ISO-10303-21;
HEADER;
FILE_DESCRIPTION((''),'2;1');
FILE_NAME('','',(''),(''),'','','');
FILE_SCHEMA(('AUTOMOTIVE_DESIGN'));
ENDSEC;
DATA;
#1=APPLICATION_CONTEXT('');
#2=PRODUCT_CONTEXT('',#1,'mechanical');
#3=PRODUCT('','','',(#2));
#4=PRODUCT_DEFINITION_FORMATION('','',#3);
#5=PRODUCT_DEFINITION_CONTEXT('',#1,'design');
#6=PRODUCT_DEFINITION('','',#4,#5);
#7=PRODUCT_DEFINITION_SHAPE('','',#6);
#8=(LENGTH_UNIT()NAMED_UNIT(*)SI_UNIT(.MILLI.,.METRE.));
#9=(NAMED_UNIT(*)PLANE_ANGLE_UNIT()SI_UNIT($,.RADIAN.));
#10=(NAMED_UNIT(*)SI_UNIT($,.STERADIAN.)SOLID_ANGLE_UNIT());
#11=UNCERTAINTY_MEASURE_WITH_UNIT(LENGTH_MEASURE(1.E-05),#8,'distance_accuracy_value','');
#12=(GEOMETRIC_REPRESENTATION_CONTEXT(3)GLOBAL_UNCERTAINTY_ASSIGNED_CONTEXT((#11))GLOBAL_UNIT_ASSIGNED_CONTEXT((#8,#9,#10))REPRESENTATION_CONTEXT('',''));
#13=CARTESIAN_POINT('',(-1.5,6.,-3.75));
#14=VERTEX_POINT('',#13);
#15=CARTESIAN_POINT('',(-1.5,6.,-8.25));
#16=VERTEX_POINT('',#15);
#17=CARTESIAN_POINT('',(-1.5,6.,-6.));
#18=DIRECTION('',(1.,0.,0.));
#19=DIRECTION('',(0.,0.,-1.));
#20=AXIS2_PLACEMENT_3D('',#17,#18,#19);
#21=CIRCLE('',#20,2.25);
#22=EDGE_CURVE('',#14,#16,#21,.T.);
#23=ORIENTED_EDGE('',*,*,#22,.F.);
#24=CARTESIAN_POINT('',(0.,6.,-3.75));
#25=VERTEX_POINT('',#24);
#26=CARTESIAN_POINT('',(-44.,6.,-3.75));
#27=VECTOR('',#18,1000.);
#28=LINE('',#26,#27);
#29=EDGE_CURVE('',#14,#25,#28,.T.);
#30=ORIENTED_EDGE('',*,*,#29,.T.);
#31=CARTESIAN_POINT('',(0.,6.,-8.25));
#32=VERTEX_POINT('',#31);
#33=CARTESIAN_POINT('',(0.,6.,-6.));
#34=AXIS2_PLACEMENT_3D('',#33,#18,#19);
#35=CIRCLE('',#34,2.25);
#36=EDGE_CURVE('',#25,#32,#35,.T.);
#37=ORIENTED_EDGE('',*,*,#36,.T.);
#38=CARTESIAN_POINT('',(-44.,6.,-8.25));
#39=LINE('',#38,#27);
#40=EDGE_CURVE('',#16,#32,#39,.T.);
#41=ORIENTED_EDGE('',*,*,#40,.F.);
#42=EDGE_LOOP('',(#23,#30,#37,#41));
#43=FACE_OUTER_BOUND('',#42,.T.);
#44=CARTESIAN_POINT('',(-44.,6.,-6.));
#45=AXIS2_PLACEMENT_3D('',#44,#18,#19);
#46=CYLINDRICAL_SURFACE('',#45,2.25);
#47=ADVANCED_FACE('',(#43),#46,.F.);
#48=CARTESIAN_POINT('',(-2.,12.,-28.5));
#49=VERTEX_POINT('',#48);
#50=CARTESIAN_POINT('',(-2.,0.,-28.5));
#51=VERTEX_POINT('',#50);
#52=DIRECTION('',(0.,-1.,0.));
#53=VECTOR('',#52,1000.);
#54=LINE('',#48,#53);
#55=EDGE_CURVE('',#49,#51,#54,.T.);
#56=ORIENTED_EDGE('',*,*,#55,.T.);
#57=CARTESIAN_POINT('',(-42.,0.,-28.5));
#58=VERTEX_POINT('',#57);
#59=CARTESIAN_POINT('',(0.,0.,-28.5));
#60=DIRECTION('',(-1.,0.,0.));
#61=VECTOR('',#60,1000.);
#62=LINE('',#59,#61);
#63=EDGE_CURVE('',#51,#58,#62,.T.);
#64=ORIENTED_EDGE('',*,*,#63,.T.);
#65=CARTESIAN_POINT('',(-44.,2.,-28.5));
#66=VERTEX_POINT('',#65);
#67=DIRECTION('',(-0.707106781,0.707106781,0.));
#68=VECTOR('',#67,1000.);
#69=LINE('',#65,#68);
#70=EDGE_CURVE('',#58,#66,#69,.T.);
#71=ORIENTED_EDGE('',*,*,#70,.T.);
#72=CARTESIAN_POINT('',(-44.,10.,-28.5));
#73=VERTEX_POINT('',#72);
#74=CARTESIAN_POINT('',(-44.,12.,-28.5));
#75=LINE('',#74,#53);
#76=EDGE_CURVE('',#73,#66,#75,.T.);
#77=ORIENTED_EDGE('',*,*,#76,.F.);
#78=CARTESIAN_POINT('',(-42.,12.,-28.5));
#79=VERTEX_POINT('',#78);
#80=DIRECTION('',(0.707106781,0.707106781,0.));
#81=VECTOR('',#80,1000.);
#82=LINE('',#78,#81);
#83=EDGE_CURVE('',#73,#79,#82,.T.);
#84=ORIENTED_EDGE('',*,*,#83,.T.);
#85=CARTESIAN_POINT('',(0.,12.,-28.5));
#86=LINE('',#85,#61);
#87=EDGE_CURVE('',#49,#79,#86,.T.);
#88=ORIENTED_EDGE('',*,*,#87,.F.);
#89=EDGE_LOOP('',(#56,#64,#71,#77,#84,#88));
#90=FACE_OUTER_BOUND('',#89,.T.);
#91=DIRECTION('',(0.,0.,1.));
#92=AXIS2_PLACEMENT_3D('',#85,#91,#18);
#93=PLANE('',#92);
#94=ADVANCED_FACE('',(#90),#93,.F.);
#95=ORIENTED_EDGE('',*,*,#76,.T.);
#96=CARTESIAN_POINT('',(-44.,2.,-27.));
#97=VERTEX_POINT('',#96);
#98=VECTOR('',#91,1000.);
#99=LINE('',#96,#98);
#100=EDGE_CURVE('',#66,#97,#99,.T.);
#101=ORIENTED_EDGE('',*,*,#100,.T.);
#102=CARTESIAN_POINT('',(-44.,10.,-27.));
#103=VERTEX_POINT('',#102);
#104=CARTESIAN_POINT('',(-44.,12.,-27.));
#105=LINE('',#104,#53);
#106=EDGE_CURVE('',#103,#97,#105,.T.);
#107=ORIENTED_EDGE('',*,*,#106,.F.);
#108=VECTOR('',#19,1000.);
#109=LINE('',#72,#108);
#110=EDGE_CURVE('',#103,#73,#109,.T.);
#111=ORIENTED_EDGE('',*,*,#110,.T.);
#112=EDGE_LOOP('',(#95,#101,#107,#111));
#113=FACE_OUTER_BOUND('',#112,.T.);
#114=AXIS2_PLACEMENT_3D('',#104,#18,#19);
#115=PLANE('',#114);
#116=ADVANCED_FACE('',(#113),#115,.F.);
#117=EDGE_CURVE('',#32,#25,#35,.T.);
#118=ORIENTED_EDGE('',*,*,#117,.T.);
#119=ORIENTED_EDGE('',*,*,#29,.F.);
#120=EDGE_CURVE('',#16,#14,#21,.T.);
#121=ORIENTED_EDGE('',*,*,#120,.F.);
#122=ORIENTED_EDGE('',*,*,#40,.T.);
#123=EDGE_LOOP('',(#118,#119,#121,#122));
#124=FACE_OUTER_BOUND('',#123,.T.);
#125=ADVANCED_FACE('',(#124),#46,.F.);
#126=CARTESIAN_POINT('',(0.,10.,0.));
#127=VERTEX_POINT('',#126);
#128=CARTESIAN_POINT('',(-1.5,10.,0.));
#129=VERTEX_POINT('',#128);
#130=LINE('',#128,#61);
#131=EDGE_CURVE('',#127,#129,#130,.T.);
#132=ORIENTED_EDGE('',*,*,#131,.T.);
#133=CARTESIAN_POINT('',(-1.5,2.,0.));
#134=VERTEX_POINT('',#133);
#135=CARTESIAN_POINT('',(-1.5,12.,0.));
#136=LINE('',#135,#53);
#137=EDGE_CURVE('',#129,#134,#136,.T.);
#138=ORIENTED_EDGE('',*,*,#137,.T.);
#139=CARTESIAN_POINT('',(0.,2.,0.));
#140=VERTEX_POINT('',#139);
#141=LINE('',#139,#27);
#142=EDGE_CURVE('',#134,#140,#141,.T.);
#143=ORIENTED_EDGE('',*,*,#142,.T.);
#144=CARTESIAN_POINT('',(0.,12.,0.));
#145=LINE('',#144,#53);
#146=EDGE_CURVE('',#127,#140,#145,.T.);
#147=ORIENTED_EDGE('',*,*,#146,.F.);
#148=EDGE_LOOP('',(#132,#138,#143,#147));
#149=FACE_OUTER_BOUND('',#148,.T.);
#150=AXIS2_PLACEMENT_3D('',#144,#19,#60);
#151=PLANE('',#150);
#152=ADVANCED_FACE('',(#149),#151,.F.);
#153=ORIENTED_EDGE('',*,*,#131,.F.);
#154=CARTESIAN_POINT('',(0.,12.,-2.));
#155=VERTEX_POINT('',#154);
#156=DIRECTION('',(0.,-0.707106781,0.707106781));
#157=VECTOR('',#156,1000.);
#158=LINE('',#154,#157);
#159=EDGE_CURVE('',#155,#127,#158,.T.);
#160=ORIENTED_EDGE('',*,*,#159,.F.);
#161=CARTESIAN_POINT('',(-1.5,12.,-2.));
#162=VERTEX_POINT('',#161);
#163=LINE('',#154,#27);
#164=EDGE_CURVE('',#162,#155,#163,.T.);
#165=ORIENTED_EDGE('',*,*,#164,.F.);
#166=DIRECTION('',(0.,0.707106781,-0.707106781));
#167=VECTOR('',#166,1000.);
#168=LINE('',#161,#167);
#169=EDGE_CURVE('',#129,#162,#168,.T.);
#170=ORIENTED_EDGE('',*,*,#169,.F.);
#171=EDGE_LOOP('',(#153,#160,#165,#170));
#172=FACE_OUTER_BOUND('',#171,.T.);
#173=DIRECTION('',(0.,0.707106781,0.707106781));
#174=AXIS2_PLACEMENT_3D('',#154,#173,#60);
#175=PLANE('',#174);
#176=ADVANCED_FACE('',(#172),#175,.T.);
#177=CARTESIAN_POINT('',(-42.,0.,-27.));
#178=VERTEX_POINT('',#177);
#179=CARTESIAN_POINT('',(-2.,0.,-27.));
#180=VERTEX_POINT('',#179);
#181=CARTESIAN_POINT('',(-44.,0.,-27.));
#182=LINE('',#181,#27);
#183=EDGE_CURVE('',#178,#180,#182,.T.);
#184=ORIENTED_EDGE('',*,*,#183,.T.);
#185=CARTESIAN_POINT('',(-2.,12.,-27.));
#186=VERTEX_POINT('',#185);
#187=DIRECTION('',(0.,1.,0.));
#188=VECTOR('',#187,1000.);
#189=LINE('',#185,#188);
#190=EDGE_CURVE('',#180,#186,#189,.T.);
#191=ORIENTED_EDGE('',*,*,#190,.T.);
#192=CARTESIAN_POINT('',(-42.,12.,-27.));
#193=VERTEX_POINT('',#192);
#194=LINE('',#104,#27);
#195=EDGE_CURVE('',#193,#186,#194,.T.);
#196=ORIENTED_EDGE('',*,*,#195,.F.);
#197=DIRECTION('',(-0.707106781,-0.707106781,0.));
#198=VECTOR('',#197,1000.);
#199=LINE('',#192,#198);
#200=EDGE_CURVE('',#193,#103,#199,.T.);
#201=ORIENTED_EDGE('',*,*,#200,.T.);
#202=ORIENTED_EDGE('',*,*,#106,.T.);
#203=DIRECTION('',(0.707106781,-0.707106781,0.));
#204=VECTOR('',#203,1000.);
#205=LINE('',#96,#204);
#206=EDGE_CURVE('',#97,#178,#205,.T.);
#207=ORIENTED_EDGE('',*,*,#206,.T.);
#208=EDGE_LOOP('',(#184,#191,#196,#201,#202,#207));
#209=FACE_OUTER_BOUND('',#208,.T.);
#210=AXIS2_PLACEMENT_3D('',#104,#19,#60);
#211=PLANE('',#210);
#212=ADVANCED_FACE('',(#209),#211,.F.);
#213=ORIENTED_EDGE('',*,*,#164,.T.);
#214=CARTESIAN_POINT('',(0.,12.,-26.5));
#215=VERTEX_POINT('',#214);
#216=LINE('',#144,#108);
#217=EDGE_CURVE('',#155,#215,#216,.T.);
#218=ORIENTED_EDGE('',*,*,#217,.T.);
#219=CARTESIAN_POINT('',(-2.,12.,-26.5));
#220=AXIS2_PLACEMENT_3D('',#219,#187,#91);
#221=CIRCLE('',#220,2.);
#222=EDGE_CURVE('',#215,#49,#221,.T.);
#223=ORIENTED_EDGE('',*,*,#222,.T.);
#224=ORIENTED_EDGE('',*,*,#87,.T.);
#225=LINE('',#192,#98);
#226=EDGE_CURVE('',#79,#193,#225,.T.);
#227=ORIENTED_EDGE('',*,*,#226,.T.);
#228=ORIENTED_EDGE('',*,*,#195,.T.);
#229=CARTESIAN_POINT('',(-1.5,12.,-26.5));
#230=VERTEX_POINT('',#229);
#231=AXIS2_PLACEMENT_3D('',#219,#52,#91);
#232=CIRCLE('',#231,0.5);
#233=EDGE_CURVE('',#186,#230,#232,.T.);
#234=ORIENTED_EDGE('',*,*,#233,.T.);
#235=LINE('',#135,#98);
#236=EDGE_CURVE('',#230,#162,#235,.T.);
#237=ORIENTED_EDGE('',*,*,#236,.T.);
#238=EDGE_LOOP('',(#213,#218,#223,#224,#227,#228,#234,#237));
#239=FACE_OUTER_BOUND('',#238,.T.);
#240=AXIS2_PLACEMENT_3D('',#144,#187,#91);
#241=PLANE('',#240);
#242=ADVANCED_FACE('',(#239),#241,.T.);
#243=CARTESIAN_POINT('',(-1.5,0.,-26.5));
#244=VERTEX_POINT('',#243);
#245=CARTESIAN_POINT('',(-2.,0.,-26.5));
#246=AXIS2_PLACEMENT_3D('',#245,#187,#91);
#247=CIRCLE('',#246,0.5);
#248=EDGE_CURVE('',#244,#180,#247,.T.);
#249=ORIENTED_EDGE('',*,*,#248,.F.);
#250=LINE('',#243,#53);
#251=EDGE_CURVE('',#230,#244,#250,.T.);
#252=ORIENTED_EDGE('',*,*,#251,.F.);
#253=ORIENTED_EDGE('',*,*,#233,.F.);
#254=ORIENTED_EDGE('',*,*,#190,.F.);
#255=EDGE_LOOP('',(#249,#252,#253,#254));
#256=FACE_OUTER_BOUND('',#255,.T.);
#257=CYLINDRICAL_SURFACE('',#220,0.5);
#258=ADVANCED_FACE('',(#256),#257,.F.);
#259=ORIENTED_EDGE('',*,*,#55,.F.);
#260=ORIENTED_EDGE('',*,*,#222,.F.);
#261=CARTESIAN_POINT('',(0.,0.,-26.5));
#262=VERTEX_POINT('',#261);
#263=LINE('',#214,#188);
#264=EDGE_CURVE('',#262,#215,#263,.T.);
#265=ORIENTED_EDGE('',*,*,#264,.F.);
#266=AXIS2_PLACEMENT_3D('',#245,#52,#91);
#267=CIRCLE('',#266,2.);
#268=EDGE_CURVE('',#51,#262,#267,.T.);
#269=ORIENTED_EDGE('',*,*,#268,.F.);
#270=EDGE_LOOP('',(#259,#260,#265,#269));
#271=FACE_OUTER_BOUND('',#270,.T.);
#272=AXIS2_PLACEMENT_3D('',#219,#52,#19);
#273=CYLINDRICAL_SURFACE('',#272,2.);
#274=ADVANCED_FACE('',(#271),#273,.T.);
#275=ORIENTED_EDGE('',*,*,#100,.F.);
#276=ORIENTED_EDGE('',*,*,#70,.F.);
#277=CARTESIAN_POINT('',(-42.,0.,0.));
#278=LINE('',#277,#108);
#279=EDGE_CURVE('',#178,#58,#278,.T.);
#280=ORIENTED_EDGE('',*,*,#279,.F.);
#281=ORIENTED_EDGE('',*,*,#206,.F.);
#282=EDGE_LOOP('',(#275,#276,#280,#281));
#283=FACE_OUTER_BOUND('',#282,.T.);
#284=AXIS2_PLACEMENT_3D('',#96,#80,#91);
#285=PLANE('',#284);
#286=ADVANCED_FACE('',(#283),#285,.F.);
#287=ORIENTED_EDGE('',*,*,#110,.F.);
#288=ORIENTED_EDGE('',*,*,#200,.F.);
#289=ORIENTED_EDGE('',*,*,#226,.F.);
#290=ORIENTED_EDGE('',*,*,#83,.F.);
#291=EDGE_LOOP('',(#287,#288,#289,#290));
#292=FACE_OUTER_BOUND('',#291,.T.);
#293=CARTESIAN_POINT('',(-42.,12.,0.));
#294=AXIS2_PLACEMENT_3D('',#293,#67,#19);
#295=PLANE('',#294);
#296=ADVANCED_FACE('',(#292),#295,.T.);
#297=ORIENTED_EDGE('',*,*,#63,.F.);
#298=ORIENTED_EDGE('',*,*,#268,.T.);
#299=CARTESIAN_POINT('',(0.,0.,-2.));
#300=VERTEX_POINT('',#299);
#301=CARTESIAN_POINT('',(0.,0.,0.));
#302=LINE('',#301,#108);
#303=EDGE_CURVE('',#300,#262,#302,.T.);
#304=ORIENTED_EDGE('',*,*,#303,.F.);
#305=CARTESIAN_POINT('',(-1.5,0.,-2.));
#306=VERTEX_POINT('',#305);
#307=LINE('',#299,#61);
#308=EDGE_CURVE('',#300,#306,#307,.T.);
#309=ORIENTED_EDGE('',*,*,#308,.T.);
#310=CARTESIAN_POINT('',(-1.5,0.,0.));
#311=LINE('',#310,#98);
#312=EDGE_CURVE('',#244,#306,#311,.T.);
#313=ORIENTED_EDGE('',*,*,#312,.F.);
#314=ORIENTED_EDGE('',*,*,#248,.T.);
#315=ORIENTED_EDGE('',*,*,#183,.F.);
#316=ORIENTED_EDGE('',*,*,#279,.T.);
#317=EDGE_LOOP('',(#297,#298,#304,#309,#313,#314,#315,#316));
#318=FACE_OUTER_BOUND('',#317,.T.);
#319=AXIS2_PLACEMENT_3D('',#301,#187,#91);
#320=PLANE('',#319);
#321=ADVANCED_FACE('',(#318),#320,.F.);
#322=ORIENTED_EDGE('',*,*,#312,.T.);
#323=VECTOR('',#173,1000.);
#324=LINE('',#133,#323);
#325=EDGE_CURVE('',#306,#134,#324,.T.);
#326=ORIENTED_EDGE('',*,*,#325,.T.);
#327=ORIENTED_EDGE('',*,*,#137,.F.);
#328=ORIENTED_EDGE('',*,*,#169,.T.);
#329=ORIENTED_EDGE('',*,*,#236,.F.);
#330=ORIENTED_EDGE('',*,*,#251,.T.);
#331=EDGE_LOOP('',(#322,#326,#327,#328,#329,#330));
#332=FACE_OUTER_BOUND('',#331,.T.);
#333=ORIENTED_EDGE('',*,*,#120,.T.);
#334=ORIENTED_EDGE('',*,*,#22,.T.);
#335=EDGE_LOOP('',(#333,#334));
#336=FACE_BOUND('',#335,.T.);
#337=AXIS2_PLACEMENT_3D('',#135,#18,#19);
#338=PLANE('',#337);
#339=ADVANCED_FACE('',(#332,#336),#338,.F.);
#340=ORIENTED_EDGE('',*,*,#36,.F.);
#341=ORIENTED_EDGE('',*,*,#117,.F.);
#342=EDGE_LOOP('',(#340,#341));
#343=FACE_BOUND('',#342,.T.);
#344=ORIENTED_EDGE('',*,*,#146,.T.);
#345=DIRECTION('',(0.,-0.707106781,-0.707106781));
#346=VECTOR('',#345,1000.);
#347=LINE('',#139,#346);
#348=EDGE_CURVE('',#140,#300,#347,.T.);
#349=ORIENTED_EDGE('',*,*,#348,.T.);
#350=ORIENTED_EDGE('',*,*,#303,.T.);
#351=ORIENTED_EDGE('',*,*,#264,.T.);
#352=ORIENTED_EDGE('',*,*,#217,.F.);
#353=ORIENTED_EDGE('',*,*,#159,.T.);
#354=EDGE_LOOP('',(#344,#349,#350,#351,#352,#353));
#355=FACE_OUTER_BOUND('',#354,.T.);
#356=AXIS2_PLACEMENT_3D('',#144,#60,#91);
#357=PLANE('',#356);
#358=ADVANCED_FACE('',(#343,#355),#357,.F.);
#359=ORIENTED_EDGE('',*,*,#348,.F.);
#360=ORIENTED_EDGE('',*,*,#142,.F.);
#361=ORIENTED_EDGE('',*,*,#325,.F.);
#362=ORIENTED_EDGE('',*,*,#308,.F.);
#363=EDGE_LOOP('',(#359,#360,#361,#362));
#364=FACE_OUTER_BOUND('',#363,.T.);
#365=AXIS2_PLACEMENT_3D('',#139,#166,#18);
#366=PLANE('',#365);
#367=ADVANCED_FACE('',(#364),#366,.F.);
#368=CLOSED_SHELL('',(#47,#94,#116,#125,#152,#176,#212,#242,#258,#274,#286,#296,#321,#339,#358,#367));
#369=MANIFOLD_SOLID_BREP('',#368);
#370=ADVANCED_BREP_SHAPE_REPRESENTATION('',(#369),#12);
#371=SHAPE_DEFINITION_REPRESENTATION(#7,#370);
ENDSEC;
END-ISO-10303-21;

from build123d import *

# Parameters (mm, degrees)
BOSS_EXTRUDE1_DEPTH = 12
SKETCH2_R           = 2.25
CUT_EXTRUDE1_DEPTH  = 54.779642989
CHAMFER1_SIZE       = 2
FILLET1_R           = 2
FILLET2_R           = 0.5


with BuildPart() as part:
    # Sketch1 → Boss-Extrude1 (new body)
    with BuildSketch(Plane(origin=(0, 0, 0), x_dir=(1, 0, 0), z_dir=(0, 1, 0))):
        Polygon((0, 0), (-1.5, 0), (-1.5, 27), (-44, 27), (-44, 28.5), (0, 28.5), align=None)
    extrude(amount=BOSS_EXTRUDE1_DEPTH)

    # Sketch2 → Cut-Extrude1 (cut, through all)
    with BuildSketch(Plane(origin=(0, 0, 0), x_dir=(0, 0, -1), z_dir=(1, 0, 0))):
        with Locations((6, 6)):
            Circle(SKETCH2_R)
    extrude(amount=-CUT_EXTRUDE1_DEPTH, mode=Mode.SUBTRACT)

    # Chamfer1
    chamfer1_edges = [part.edges().sort_by_distance(p)[0] for p in [
        (-44, 12, -27.75),
        (-0.75, 12, 0),
        (-0.75, 0, 0),
        (-44, 0, -27.75),
    ]]
    chamfer(chamfer1_edges, length=CHAMFER1_SIZE)

    # Fillet1
    fillet1_edges = [part.edges().sort_by_distance(p)[0] for p in [
        (0, 6, -28.5),
    ]]
    fillet(fillet1_edges, radius=FILLET1_R)

    # Fillet2
    fillet2_edges = [part.edges().sort_by_distance(p)[0] for p in [
        (-1.5, 6, -27),
    ]]
    fillet(fillet2_edges, radius=FILLET2_R)


solid = part.part
